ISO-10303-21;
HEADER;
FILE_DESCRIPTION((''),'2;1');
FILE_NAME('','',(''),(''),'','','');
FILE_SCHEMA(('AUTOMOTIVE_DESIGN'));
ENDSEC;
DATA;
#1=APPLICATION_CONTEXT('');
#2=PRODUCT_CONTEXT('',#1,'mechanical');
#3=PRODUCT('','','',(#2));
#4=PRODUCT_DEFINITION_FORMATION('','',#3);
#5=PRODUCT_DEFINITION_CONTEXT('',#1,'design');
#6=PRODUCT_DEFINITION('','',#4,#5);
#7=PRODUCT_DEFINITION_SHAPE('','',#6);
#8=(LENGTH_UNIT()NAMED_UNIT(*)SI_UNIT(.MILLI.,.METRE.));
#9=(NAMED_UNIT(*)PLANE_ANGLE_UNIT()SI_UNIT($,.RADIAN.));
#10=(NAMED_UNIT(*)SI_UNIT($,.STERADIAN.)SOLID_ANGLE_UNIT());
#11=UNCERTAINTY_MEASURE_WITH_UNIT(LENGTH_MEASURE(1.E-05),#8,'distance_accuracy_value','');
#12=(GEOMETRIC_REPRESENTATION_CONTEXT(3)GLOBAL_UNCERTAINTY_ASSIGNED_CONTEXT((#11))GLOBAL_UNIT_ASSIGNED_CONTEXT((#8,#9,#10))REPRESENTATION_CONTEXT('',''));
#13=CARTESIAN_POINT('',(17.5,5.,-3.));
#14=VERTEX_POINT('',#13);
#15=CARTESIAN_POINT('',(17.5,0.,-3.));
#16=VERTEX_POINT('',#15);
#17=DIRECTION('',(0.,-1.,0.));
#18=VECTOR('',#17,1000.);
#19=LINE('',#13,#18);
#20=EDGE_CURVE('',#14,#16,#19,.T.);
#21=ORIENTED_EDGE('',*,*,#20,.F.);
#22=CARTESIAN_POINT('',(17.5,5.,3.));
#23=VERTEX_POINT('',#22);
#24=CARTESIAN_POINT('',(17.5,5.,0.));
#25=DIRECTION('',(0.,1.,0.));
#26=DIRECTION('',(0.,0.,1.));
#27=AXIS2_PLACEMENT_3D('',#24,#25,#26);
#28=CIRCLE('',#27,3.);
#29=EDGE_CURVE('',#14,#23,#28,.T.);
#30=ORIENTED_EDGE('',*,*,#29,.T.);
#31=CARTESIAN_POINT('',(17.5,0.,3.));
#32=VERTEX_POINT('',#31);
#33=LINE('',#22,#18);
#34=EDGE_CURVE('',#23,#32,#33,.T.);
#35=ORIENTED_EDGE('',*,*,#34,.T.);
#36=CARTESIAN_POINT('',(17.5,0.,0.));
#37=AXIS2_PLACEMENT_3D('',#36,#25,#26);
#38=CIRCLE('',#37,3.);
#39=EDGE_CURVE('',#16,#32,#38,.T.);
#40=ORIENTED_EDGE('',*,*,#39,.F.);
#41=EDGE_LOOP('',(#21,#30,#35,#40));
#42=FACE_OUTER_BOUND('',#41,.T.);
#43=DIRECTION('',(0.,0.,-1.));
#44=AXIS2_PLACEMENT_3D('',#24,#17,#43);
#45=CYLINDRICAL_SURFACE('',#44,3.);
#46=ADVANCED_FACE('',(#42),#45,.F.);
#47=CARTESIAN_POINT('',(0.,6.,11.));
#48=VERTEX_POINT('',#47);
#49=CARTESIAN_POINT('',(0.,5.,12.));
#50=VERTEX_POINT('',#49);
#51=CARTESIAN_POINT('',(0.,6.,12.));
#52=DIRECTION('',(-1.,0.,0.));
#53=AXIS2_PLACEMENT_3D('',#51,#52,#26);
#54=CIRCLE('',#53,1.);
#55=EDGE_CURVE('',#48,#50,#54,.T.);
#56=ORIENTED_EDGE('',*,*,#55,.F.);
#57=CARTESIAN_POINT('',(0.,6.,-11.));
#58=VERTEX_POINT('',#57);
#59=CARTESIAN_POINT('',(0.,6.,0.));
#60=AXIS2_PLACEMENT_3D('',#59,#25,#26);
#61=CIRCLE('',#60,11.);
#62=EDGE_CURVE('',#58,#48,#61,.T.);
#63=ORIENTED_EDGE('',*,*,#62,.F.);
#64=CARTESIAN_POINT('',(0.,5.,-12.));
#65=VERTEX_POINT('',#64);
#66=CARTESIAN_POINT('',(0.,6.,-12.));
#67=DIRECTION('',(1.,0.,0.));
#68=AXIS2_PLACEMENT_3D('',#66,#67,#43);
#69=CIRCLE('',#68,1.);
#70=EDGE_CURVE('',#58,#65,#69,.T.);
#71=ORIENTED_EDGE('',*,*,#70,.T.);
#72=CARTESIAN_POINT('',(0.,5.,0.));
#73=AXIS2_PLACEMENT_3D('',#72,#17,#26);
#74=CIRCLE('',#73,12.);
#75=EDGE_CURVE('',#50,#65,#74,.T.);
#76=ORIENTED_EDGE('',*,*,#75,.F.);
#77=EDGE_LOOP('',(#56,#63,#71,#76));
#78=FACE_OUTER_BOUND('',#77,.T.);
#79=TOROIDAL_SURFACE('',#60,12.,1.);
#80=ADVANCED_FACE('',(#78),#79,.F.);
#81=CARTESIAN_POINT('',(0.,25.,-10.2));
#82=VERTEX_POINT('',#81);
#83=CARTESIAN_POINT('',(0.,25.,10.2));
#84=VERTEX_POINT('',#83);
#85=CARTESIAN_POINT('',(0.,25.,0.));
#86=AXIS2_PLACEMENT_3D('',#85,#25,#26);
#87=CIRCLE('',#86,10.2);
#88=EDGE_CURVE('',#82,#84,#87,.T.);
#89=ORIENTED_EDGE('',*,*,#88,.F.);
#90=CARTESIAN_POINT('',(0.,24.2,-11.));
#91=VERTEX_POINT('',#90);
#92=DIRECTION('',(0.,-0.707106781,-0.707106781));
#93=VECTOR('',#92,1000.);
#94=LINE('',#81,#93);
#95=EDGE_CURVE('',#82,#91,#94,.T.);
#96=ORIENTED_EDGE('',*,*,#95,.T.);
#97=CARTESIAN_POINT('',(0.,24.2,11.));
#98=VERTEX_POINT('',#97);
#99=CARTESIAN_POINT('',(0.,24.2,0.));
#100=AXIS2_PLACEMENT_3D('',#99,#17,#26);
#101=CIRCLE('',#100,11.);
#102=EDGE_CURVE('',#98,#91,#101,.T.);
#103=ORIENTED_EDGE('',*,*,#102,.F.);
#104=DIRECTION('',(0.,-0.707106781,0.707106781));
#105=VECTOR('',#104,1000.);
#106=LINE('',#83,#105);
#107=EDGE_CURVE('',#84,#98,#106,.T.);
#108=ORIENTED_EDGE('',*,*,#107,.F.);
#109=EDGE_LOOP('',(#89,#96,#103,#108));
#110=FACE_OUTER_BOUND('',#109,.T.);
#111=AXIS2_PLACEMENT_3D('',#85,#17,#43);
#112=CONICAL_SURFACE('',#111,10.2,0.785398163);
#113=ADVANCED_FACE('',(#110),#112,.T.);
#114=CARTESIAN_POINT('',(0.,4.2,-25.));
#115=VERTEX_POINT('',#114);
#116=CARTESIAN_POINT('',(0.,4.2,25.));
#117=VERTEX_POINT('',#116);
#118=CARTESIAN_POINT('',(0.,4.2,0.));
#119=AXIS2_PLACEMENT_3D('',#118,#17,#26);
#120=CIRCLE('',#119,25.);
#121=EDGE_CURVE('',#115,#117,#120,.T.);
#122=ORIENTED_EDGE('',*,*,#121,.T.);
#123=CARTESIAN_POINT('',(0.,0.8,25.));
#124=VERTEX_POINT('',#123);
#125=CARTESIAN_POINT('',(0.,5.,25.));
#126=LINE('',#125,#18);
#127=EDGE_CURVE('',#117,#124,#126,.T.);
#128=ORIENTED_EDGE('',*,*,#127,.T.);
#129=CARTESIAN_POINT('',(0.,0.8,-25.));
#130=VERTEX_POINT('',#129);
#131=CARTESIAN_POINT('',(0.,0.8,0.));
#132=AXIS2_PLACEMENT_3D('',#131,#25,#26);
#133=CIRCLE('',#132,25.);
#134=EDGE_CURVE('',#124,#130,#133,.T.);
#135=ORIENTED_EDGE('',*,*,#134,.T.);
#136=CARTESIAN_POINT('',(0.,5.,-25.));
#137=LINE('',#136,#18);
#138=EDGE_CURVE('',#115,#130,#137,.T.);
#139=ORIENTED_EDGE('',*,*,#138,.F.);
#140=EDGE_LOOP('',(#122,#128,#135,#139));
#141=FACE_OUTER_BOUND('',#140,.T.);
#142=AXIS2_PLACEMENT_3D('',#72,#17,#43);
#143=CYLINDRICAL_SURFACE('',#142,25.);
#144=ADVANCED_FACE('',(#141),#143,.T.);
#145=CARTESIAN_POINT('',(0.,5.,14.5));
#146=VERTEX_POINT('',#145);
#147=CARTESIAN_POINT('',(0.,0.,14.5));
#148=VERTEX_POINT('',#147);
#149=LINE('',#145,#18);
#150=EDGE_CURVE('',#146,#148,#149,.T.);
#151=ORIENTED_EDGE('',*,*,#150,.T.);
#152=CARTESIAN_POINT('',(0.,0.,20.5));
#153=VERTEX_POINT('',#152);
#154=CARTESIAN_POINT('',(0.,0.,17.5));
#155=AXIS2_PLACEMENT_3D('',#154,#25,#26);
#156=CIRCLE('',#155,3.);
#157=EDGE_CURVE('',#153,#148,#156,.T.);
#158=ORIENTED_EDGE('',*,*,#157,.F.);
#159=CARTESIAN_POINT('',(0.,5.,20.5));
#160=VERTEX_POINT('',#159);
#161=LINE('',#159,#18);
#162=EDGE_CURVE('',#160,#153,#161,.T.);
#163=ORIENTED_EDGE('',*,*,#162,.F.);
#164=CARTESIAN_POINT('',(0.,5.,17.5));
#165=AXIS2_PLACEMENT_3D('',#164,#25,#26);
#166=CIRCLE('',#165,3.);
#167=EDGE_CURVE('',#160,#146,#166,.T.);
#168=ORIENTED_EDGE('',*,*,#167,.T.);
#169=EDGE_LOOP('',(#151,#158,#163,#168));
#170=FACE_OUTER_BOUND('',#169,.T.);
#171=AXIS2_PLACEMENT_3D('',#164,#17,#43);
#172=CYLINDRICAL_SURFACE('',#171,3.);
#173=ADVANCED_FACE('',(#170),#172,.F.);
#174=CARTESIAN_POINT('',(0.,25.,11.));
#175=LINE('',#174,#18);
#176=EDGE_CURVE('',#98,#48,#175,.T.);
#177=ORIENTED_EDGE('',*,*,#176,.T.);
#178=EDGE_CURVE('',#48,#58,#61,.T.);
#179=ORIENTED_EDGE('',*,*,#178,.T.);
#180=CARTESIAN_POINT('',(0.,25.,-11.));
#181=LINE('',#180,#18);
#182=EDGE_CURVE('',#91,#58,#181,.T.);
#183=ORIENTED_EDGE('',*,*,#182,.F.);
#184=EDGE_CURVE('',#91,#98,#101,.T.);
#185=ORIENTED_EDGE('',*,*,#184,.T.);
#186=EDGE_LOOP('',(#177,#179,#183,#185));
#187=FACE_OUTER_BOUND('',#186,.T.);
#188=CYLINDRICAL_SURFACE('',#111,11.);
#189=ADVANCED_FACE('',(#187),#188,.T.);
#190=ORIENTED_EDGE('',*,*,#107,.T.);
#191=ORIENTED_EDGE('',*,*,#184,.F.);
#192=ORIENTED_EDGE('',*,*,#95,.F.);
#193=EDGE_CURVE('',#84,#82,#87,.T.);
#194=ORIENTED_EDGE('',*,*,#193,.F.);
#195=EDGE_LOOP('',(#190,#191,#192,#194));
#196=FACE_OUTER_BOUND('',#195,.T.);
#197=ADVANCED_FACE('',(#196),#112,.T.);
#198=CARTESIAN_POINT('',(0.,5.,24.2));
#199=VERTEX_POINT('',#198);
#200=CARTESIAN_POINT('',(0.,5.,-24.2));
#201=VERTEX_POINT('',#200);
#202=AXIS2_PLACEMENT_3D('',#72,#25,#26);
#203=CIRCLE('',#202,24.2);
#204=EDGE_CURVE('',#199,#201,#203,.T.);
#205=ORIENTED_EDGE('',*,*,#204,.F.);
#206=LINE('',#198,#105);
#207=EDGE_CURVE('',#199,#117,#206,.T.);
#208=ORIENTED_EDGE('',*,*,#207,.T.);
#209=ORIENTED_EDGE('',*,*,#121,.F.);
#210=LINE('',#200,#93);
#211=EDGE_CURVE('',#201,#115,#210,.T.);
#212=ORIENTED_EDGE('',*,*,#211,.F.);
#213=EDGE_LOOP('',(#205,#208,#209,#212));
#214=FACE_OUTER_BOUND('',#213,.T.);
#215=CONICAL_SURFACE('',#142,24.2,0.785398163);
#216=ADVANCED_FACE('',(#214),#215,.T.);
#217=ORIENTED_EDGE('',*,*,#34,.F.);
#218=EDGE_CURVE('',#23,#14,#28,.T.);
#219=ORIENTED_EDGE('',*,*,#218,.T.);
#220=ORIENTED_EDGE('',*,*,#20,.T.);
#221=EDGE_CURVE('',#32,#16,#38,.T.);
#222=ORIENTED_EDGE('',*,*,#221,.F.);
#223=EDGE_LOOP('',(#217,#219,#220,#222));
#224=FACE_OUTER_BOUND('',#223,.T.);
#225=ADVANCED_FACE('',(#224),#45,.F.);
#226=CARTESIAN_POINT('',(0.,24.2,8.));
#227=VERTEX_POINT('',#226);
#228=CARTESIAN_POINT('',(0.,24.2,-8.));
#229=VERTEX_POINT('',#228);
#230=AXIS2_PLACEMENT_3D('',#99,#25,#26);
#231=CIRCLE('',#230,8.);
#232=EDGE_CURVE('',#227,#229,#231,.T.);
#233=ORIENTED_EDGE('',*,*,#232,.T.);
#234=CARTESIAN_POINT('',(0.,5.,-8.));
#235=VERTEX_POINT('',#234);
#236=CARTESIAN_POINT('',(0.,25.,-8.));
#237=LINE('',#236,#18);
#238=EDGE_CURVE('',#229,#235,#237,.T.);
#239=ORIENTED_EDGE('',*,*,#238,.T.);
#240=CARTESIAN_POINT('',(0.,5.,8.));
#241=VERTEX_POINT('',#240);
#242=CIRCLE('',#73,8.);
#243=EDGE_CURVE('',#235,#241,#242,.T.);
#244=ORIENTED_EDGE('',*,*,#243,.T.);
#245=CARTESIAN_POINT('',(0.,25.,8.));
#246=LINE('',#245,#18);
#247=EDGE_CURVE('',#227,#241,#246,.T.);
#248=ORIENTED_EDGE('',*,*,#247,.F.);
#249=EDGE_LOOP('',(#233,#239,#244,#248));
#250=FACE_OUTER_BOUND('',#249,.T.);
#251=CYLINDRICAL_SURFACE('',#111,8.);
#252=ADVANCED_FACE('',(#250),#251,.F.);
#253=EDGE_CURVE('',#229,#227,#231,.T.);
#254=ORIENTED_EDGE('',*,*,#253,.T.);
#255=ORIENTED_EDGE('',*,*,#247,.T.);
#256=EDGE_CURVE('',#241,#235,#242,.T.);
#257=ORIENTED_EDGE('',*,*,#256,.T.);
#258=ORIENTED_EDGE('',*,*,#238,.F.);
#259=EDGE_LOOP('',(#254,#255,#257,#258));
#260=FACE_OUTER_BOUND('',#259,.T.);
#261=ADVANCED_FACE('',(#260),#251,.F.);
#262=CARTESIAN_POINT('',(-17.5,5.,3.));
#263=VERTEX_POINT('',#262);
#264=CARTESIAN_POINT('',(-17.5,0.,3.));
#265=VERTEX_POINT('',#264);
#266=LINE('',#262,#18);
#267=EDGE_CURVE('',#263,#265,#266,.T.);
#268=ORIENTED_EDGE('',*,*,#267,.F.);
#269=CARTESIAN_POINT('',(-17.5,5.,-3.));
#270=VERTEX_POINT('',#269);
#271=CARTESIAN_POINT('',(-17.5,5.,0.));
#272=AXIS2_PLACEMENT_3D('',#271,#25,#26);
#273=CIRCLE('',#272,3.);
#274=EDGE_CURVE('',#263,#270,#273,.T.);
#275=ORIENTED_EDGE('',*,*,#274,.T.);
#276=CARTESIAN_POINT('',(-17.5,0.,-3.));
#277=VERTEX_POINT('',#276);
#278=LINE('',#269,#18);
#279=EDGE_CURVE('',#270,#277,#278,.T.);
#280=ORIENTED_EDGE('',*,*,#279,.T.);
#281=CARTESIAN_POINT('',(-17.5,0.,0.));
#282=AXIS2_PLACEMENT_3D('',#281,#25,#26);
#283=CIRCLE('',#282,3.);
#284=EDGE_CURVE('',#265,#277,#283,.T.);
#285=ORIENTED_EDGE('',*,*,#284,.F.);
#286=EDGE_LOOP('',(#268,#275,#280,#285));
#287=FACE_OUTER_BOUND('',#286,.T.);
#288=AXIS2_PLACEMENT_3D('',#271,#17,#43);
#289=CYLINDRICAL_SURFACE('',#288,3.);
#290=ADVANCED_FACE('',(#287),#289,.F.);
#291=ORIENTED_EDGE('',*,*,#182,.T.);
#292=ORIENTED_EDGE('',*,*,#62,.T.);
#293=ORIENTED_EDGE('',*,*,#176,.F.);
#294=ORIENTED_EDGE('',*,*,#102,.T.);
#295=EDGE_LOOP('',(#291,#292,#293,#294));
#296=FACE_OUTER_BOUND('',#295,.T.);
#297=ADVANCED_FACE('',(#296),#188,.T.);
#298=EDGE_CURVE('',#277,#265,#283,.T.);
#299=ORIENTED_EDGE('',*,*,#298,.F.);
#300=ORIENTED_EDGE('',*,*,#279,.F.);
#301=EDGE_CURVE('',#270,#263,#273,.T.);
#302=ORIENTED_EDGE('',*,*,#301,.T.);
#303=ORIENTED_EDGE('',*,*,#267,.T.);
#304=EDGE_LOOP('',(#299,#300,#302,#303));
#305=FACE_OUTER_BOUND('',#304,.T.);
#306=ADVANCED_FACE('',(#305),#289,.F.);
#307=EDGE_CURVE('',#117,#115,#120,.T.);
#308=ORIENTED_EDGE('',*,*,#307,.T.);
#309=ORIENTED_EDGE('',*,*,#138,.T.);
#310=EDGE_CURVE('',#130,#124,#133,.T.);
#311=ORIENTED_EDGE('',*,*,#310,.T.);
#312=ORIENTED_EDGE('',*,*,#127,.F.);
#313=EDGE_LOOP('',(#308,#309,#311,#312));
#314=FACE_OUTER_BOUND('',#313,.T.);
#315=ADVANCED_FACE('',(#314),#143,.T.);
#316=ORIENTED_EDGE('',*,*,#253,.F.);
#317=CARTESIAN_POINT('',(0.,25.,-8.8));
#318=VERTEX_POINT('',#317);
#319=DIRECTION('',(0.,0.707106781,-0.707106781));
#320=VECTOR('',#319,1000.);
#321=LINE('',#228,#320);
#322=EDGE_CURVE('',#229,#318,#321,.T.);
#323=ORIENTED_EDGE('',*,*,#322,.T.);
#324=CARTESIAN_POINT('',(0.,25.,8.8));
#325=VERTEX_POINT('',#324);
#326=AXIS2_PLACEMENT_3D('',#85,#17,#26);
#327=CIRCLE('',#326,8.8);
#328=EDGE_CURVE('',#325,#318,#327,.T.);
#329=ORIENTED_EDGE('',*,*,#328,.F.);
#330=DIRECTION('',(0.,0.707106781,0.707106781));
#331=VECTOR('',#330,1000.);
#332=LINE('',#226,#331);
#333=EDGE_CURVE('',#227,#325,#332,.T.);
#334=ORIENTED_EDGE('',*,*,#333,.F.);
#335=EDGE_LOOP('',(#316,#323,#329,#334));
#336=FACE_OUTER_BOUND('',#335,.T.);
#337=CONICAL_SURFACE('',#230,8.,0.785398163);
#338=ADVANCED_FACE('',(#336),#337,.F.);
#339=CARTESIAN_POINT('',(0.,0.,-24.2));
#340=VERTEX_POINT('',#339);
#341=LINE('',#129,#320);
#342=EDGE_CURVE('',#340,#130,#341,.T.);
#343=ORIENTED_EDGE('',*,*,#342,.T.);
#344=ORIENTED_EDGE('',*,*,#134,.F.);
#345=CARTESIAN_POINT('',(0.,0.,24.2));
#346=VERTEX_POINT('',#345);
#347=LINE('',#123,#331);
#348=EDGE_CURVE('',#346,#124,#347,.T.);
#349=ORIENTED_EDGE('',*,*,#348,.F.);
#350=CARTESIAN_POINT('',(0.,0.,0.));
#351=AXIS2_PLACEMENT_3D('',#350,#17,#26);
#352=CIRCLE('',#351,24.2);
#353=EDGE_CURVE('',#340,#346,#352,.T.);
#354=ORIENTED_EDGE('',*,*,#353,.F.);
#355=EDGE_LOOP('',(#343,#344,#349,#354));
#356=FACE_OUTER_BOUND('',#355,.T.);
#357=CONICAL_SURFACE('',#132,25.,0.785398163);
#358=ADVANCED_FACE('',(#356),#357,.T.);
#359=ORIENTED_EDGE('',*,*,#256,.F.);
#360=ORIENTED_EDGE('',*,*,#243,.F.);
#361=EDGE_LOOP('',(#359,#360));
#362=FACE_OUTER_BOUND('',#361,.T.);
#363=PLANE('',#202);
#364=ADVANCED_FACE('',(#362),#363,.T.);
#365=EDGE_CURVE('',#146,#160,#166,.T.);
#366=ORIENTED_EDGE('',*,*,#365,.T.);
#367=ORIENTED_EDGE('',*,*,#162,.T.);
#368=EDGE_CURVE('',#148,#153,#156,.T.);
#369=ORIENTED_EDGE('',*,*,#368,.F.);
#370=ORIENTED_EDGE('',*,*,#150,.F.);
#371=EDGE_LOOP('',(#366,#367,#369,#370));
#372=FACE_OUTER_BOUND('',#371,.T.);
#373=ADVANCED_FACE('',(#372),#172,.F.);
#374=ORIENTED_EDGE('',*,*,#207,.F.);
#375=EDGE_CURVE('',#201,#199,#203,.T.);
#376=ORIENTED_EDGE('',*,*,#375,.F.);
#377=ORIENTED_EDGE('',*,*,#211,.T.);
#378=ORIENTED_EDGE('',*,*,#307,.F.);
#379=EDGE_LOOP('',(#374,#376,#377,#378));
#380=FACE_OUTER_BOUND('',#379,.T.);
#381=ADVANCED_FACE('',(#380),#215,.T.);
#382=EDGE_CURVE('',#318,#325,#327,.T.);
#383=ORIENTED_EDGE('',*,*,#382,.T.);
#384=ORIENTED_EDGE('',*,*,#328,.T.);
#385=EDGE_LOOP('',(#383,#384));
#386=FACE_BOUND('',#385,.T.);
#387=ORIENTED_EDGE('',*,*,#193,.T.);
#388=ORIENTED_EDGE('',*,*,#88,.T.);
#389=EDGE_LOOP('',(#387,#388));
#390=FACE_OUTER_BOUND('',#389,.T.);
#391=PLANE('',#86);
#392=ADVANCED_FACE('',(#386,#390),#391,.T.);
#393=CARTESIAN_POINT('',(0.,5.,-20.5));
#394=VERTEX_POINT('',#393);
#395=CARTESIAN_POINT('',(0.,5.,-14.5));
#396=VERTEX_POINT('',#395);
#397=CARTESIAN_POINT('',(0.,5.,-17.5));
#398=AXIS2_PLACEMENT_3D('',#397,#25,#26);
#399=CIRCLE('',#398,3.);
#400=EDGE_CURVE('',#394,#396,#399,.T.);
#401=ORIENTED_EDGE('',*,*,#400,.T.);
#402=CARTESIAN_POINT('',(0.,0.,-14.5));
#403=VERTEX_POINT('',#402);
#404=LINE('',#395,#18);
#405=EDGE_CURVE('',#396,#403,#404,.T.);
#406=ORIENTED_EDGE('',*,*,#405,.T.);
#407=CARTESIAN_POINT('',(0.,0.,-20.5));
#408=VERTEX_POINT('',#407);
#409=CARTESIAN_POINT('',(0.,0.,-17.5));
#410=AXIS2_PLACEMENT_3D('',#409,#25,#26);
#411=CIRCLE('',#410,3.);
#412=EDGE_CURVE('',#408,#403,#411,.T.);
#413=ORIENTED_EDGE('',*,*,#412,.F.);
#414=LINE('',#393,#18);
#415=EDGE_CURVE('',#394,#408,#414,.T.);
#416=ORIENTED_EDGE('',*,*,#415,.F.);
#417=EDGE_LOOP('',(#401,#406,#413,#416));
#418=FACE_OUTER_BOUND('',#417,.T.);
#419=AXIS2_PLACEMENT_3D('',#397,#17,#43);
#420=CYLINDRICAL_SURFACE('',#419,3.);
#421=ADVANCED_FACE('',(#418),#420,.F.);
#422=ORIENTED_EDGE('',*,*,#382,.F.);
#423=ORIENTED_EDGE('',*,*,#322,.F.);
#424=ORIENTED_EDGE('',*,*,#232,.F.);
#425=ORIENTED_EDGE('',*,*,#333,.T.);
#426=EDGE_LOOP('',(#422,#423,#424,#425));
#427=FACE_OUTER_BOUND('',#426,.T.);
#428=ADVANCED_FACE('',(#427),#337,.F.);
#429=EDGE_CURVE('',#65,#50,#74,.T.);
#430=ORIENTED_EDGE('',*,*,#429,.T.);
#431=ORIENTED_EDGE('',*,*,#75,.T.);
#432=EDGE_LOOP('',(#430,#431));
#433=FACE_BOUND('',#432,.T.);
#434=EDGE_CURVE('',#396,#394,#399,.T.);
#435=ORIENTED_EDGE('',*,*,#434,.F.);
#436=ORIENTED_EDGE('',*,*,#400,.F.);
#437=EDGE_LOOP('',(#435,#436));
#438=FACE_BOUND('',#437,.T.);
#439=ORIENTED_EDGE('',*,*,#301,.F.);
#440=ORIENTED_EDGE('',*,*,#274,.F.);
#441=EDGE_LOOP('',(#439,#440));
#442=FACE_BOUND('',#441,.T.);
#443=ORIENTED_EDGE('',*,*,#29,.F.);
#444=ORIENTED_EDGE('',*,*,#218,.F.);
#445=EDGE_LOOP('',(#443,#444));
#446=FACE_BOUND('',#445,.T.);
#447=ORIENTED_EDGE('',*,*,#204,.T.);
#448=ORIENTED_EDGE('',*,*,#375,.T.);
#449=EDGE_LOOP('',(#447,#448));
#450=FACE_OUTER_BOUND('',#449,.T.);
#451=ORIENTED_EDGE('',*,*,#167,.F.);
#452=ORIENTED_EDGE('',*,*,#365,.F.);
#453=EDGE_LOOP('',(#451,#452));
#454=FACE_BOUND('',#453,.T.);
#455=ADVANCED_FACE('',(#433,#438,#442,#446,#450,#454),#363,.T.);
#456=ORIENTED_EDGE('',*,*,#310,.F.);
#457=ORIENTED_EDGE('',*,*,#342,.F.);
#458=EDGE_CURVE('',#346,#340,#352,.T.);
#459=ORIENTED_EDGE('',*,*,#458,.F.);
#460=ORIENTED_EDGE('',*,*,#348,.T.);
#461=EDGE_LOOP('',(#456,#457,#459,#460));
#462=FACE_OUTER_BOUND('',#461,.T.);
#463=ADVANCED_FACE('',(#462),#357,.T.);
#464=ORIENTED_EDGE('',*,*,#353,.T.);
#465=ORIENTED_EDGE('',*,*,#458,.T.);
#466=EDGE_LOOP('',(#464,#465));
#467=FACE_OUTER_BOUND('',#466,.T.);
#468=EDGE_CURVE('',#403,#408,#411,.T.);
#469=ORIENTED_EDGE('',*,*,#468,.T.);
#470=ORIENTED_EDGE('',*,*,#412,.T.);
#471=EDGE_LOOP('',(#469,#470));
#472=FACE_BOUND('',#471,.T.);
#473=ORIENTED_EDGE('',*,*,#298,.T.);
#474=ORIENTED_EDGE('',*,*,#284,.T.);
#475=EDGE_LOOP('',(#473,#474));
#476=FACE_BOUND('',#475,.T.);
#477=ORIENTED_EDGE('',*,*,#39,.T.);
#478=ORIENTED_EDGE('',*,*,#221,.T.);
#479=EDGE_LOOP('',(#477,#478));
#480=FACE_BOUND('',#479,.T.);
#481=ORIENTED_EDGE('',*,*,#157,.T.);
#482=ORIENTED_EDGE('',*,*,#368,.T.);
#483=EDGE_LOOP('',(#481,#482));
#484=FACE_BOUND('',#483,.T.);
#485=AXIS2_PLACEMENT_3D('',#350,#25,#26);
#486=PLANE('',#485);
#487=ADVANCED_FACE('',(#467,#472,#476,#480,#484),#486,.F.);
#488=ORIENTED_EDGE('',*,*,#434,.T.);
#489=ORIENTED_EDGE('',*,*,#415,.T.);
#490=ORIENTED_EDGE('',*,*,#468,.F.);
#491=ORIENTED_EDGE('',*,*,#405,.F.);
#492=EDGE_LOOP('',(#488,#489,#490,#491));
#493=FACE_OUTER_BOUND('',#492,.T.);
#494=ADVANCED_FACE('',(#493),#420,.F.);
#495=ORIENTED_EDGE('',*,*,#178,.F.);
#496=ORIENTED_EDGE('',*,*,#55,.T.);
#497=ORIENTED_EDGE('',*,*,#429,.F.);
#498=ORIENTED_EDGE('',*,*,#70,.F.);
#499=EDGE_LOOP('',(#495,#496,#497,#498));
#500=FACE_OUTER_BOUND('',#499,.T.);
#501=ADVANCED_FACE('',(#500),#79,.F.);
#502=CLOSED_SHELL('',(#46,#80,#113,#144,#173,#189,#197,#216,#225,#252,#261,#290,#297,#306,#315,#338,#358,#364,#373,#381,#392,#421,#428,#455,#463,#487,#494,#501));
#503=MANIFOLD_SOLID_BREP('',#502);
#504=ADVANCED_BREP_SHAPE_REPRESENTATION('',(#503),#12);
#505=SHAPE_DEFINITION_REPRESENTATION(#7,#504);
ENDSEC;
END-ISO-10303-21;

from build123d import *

# Parameters (mm, degrees)
SKETCH1_R           = 25
BOSS_EXTRUDE2_DEPTH = 5
SKETCH3_R           = 3
CUT_EXTRUDE2_DEPTH  = 5
SKETCH4_R           = 11
SKETCH4_R_2         = 8
BOSS_EXTRUDE3_DEPTH = 20
CHAMFER1_SIZE       = 0.8
FILLET1_R           = 1


with BuildPart() as part:
    # Sketch1 → Boss-Extrude2 (new body)
    with BuildSketch(Plane(origin=(0, 0, 0), x_dir=(1, 0, 0), z_dir=(0, 1, 0))):
        with Locations(Location((0, 0, 0), (0, 0, 270))):
            Circle(SKETCH1_R)
    extrude(amount=BOSS_EXTRUDE2_DEPTH)

    # Sketch3 → Cut-Extrude2 (cut)
    with BuildSketch(Plane(origin=(0, 0, 0), x_dir=(1, 0, 0), z_dir=(0, 1, 0))):
        with Locations(Location((-17.5, 0, 0), (0, 0, 270))):
            Circle(SKETCH3_R)
        with Locations(Location((0, 17.5, 0), (0, 0, 270))):
            Circle(SKETCH3_R)
        with Locations(Location((17.5, 0, 0), (0, 0, 270))):
            Circle(SKETCH3_R)
        with Locations(Location((0, -17.5, 0), (0, 0, 270))):
            Circle(SKETCH3_R)
    extrude(amount=CUT_EXTRUDE2_DEPTH, mode=Mode.SUBTRACT)

    # Sketch4 → Boss-Extrude3 (add)
    with BuildSketch(Plane(origin=(0, 5, 0), x_dir=(1, 0, 0), z_dir=(0, 1, 0))):
        with Locations(Location((0, 0, 0), (0, 0, 270))):
            Circle(SKETCH4_R)
        with Locations(Location((0, 0, 0), (0, 0, 270))):
            Circle(SKETCH4_R_2, mode=Mode.SUBTRACT)
    extrude(amount=BOSS_EXTRUDE3_DEPTH)

    # Chamfer1
    chamfer1_edges = [part.edges().sort_by_distance(p)[0] for p in [
        (0, 0, -25),
        (0, 25, -11),
        (0, 25, -8),
        (0, 5, -25),
    ]]
    chamfer(chamfer1_edges, length=CHAMFER1_SIZE)

    # Fillet1
    fillet1_edges = [part.edges().sort_by_distance(p)[0] for p in [
        (0, 5, -11),
    ]]
    fillet(fillet1_edges, radius=FILLET1_R)


solid = part.part
